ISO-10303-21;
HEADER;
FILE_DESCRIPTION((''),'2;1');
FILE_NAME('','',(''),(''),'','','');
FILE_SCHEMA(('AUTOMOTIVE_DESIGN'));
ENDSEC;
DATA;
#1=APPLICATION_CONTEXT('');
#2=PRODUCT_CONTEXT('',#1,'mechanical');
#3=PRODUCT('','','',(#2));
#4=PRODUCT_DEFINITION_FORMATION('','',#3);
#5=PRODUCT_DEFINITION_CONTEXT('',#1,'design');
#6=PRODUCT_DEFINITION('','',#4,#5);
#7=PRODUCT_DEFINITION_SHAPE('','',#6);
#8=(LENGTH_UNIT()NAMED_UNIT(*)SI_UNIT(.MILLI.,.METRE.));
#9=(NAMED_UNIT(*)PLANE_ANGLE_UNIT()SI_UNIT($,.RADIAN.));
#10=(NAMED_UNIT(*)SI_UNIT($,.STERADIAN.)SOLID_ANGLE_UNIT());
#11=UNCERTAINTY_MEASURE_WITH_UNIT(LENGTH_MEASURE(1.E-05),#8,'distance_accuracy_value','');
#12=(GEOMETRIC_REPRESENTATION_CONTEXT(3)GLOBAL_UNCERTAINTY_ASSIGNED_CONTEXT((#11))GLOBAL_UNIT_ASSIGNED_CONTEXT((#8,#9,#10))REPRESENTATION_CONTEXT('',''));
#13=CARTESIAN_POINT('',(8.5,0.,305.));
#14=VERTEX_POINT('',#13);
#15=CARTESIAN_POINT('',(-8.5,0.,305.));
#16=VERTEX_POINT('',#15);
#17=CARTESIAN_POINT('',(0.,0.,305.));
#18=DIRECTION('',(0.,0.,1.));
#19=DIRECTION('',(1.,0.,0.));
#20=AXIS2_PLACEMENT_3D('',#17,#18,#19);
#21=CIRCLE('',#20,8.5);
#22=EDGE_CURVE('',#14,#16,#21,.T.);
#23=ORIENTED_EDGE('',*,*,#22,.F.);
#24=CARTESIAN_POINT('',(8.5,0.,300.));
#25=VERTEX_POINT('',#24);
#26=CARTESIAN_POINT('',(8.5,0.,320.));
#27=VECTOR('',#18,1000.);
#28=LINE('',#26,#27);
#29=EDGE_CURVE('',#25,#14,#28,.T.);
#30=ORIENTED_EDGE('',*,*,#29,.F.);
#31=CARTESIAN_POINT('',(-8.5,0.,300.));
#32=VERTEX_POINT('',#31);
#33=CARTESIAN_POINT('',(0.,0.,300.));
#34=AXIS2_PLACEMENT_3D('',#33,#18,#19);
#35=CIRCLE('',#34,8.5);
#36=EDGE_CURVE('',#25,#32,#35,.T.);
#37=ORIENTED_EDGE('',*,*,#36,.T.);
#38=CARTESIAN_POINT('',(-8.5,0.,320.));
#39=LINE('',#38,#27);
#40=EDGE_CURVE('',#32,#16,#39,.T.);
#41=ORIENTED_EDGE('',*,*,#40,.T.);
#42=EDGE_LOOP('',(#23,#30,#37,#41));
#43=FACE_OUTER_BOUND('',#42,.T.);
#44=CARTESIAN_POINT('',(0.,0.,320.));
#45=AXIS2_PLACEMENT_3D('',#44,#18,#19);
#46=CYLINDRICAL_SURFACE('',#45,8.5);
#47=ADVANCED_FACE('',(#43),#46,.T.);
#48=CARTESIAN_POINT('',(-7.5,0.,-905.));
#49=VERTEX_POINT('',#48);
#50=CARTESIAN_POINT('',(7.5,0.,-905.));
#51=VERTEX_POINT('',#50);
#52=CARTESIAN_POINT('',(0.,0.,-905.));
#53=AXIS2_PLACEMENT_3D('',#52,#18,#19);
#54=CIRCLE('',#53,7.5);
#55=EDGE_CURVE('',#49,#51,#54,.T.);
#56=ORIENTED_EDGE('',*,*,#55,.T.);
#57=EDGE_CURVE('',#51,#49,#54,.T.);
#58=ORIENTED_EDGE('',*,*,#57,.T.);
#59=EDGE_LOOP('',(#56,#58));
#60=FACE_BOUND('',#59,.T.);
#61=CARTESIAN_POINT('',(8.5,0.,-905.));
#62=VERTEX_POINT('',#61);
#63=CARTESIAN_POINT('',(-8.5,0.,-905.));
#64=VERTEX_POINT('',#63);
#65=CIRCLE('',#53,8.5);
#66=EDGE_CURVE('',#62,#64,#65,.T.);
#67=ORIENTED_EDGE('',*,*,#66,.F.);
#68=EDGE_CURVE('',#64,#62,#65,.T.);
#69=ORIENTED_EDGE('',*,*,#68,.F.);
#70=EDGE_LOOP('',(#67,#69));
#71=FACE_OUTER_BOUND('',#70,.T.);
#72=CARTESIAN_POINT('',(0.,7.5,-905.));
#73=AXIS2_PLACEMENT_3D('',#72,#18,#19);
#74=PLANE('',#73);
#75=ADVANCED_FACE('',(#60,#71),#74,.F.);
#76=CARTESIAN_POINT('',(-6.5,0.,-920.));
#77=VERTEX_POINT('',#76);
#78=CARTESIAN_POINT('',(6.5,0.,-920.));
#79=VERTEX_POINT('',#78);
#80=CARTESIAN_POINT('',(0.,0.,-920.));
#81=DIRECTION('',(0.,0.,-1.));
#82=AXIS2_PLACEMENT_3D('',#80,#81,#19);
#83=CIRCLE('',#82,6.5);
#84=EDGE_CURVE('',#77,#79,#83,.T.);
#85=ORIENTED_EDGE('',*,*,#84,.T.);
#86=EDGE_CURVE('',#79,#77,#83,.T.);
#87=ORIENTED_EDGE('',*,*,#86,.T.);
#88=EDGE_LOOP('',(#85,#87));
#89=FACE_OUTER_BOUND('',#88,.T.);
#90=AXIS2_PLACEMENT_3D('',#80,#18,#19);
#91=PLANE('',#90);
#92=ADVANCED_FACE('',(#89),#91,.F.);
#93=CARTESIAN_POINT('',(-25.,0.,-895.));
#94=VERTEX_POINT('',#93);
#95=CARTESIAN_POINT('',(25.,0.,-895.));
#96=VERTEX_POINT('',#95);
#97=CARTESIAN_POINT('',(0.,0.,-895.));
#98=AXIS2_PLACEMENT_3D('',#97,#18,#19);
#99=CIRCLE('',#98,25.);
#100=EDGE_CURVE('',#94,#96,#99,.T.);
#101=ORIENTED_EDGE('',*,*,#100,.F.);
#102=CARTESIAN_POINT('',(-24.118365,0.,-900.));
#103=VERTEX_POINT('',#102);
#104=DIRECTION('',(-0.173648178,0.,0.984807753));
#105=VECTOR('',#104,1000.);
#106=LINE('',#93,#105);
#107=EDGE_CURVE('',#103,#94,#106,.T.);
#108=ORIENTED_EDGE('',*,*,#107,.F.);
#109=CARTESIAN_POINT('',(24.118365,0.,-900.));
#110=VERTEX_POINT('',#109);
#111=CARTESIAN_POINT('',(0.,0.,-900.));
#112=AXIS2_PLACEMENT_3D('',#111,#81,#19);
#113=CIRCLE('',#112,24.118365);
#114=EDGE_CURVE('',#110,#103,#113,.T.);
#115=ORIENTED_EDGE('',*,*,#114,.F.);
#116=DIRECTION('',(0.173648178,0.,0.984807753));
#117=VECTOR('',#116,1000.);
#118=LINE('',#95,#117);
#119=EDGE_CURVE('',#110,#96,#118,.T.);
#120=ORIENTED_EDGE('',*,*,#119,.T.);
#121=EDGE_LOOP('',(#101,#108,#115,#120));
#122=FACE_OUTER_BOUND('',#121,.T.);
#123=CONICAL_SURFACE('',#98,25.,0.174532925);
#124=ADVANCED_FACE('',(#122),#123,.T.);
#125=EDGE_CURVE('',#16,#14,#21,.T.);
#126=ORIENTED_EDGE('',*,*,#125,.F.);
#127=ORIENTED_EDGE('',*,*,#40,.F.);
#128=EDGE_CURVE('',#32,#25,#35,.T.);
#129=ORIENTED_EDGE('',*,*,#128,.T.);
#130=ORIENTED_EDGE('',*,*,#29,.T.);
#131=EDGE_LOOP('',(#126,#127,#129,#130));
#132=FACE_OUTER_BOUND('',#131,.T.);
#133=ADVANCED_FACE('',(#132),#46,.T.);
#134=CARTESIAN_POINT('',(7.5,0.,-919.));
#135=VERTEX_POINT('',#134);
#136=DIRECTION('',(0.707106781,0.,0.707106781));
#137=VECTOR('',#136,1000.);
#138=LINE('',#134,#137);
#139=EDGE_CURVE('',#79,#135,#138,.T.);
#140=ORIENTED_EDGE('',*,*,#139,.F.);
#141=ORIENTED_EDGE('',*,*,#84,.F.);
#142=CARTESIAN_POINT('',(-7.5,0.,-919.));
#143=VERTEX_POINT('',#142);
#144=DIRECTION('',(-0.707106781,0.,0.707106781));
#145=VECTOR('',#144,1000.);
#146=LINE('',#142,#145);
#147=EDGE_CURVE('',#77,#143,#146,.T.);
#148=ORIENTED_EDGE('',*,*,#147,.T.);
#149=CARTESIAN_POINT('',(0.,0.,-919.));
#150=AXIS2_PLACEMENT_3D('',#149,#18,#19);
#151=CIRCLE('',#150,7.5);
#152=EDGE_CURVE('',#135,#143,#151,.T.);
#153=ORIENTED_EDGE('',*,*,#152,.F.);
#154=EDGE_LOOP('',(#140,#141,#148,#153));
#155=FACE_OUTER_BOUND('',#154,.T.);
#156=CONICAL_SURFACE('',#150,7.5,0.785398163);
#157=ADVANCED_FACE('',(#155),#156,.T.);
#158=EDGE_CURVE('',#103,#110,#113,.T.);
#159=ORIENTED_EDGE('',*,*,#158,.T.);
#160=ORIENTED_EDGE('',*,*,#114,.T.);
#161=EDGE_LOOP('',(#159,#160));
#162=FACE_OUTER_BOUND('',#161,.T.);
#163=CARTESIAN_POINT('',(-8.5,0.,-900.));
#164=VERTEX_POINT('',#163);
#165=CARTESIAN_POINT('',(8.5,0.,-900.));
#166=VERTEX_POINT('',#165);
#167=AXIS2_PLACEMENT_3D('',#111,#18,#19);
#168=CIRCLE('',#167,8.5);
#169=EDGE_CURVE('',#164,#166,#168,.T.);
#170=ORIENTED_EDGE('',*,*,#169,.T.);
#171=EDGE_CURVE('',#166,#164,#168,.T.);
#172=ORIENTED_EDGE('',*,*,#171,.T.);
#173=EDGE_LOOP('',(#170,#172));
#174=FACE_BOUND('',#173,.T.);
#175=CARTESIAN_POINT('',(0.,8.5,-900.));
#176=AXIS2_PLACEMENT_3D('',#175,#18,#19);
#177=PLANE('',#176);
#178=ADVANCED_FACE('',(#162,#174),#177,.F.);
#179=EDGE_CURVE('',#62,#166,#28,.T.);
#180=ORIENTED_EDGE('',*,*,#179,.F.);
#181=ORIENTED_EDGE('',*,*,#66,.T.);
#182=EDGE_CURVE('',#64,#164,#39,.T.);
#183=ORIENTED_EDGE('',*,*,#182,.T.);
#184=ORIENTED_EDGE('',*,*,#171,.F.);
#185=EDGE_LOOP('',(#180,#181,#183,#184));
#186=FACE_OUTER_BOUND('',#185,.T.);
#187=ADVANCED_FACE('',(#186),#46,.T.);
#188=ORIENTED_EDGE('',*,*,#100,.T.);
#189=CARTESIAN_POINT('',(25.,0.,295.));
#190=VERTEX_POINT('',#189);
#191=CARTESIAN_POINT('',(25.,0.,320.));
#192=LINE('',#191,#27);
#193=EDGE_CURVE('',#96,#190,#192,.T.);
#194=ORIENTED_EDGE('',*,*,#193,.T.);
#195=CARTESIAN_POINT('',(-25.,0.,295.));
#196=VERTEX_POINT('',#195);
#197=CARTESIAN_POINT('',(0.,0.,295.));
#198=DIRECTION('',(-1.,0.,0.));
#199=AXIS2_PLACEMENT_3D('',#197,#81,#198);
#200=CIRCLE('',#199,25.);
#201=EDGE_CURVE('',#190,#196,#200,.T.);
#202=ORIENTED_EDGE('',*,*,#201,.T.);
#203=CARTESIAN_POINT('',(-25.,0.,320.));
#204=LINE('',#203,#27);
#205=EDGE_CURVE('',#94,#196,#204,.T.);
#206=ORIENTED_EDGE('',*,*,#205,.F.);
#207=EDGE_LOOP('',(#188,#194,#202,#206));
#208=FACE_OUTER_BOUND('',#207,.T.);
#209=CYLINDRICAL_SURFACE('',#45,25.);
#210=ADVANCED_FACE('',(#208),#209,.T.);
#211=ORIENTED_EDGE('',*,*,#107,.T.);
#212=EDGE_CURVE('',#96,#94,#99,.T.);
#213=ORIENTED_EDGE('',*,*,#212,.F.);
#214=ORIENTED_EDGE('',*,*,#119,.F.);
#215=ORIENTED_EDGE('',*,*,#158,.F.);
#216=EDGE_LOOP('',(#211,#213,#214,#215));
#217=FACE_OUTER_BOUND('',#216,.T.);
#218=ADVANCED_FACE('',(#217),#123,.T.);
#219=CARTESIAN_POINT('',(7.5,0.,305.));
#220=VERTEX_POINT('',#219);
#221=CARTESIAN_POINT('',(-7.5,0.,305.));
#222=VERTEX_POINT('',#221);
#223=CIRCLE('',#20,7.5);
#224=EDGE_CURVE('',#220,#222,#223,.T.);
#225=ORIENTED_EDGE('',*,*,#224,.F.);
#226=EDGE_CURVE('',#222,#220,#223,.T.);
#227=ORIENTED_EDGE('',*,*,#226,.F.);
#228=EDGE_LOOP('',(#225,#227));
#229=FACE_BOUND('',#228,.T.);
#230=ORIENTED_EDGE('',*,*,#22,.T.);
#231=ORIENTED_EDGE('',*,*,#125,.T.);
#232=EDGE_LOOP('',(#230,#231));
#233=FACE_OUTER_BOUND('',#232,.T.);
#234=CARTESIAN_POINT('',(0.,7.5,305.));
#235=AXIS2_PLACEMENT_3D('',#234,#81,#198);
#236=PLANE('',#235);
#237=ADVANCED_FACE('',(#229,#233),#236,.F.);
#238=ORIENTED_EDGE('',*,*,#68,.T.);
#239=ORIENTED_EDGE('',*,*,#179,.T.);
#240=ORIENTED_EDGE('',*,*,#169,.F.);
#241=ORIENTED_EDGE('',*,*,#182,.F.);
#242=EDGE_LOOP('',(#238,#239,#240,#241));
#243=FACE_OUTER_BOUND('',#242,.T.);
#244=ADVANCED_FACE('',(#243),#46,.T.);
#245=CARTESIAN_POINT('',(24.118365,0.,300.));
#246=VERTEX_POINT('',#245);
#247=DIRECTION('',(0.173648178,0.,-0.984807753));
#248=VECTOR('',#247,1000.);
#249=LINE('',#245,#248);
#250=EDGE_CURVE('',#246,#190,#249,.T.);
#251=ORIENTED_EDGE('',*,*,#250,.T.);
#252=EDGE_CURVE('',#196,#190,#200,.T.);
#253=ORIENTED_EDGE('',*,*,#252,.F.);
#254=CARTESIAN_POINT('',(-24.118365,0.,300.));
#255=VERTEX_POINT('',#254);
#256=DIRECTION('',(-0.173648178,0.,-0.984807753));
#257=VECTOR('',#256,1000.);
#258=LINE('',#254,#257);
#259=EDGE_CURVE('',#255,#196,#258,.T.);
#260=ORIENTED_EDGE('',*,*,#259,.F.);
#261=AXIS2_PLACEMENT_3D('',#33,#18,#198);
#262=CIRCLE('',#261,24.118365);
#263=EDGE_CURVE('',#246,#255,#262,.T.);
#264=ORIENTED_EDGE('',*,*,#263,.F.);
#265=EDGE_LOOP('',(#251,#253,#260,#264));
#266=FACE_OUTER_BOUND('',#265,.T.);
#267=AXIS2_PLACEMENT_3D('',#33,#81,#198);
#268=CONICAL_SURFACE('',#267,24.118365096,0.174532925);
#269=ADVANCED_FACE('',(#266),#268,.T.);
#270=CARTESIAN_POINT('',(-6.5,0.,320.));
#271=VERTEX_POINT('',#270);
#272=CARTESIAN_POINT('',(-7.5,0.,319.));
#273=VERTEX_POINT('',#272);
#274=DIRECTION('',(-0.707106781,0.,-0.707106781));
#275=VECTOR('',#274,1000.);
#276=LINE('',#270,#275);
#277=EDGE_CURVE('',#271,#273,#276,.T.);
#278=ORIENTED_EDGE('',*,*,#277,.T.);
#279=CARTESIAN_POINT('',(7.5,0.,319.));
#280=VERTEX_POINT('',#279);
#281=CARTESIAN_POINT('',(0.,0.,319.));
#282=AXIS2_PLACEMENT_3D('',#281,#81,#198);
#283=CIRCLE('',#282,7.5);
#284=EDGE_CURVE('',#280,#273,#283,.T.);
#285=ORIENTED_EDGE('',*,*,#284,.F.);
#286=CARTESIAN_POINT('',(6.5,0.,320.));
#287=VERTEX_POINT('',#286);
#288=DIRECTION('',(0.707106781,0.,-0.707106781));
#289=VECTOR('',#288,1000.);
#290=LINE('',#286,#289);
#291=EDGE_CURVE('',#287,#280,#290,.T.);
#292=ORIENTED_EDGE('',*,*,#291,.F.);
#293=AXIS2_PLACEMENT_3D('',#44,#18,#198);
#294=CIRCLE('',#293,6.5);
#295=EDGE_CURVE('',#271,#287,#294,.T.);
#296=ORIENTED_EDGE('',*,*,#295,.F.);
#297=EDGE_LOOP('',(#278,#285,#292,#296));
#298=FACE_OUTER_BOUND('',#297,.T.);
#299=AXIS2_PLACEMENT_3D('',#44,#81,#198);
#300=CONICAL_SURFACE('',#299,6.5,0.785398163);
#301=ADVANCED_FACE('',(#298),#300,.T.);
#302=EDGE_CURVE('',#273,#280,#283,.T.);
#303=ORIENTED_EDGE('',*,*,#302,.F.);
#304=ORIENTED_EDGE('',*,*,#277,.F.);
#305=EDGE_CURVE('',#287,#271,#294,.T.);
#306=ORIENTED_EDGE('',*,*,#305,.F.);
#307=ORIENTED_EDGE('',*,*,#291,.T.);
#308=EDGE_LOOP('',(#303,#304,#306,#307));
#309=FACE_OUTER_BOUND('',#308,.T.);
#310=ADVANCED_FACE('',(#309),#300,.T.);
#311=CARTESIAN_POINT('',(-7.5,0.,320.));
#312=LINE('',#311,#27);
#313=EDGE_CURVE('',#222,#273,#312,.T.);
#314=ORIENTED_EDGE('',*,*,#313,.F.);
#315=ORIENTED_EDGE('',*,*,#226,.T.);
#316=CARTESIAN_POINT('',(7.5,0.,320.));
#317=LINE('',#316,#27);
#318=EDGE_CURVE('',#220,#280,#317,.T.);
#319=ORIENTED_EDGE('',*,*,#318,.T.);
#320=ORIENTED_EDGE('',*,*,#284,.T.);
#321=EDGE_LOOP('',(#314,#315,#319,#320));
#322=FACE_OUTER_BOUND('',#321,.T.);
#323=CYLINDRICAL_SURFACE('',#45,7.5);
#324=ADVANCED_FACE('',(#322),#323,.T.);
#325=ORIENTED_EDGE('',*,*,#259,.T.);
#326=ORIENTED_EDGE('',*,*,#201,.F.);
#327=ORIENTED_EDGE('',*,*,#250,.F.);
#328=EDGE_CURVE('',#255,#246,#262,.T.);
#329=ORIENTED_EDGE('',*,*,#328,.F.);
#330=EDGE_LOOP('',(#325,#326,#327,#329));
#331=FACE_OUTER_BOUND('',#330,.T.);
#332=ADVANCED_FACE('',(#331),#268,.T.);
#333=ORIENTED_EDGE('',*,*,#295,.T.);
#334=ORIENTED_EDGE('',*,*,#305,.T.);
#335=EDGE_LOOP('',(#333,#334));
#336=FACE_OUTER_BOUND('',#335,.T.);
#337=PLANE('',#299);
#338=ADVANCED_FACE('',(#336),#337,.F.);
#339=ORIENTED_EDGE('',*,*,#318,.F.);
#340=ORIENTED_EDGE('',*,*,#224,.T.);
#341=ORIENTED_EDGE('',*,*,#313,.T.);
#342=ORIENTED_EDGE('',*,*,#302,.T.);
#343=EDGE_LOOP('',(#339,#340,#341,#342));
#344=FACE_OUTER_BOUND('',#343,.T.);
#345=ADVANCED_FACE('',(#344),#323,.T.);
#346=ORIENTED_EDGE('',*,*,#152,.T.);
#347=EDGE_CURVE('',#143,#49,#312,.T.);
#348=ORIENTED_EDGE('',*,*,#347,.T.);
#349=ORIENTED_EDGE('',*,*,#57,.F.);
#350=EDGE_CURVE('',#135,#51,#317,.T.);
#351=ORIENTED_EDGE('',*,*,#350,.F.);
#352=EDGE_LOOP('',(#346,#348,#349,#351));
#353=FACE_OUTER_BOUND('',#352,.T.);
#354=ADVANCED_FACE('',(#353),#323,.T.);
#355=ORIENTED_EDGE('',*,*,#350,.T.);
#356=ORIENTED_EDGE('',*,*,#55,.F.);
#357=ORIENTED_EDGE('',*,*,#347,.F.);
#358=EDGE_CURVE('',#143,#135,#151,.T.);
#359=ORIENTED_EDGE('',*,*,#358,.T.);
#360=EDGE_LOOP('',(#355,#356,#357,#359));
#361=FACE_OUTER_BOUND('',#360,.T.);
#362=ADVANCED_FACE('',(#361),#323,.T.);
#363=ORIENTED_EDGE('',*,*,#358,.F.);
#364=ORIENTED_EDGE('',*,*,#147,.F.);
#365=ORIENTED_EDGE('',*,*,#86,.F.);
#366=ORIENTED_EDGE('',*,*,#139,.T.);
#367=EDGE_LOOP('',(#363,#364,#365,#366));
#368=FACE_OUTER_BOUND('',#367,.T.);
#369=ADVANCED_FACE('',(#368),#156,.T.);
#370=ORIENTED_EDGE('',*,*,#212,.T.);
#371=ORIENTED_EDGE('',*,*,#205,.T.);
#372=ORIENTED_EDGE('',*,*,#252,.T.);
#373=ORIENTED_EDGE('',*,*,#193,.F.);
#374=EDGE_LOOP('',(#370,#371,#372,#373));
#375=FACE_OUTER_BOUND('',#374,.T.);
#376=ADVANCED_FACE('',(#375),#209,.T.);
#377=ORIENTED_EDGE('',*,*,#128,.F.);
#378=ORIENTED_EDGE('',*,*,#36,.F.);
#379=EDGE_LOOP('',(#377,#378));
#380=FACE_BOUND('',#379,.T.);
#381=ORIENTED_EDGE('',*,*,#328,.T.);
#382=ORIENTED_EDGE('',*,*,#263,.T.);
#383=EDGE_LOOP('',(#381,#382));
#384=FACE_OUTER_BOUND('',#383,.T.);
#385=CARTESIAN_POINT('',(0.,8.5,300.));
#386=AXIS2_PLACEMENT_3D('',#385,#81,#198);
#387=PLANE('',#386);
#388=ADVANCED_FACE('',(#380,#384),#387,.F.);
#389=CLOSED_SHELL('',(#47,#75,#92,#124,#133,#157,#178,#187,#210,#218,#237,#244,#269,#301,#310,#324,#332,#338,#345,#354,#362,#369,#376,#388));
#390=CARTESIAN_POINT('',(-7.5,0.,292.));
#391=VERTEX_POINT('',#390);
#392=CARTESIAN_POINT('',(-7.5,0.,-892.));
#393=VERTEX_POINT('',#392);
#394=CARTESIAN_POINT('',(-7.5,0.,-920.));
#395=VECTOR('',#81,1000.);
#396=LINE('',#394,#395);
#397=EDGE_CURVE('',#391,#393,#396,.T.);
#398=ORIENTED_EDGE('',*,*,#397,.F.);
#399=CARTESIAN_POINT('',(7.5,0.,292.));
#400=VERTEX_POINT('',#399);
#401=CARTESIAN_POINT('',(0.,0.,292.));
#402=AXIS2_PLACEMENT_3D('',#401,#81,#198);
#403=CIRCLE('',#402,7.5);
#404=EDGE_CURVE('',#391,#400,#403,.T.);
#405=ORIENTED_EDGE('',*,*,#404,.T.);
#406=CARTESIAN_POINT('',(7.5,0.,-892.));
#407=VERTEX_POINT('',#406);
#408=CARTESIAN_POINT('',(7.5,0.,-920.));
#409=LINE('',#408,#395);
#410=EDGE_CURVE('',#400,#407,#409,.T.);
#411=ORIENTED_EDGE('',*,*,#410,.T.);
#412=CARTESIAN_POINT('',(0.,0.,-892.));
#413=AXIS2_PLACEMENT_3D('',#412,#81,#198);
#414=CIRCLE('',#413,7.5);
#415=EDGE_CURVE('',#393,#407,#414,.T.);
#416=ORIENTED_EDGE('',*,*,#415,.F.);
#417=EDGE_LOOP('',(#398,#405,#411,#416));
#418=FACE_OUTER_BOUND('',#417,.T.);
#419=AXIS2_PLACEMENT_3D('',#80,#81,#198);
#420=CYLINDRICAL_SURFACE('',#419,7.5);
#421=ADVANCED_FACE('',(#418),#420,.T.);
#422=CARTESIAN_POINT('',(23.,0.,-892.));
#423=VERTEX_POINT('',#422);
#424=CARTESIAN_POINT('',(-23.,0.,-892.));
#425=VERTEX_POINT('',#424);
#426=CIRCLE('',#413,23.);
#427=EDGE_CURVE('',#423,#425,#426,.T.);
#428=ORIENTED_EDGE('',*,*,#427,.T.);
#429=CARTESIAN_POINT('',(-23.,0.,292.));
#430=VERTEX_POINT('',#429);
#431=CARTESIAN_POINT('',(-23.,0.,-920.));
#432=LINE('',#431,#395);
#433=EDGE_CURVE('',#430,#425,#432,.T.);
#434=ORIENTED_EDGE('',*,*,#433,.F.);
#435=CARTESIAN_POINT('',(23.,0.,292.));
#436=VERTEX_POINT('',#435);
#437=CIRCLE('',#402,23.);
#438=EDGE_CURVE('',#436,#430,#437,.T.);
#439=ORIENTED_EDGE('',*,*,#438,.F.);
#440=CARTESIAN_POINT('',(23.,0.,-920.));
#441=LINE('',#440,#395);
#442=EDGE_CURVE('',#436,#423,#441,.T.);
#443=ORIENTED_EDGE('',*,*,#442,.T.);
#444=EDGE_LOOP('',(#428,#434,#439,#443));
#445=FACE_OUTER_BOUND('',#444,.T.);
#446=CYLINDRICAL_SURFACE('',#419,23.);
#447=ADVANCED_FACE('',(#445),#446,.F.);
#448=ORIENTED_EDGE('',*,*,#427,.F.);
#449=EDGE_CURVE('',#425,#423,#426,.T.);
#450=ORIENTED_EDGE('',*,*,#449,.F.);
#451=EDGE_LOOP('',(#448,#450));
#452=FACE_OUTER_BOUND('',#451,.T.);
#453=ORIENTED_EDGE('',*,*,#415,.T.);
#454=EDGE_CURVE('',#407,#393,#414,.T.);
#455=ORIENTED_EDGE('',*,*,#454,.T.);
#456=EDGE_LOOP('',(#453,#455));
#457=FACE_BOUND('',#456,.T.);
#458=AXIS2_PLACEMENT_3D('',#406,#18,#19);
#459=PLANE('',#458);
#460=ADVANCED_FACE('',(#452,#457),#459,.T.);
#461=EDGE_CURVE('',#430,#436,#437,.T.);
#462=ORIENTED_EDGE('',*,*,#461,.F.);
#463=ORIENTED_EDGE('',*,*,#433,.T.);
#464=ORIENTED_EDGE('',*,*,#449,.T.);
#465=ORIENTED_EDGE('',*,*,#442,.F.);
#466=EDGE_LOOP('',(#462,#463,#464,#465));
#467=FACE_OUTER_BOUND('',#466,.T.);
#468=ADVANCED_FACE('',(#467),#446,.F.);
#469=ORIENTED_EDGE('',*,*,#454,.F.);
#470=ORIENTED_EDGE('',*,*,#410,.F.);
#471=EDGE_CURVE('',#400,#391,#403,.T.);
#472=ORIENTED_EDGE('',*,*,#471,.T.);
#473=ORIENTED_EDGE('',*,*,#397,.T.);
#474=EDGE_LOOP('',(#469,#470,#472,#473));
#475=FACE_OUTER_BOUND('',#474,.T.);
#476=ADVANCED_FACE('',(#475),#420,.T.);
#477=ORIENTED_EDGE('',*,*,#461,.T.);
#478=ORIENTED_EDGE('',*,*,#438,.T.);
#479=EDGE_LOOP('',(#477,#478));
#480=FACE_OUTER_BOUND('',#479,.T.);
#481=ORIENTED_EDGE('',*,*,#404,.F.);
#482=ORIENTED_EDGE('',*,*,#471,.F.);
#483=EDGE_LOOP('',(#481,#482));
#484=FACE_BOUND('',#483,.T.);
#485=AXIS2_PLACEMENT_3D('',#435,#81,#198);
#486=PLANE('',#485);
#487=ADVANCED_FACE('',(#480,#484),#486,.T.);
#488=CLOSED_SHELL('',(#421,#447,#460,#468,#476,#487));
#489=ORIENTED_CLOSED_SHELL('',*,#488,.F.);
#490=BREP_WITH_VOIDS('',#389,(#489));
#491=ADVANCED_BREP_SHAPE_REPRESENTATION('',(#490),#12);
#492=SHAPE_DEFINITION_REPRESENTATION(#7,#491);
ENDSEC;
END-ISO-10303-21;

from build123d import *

# Parameters (mm, degrees)
CHAMFER1_SIZE  = 5
CHAMFER1_SIZE2 = 0.881634904
CHAMFER2_SIZE  = 1
SKETCH5_W      = 15.5
SKETCH5_H      = 1184


with BuildPart() as part:
    # Sketch3 → Revolve1 (revolve)
    with BuildSketch(Plane(origin=(0, 0, 0), x_dir=(0, 0, -1), z_dir=(1, 0, 0)), mode=Mode.PRIVATE) as revolve1_sk:
        Polygon((-300, 25), (900, 25), (900, 8.5), (905, 8.5), (905, 7.5), (920, 7.5), (920, 0), (-320, 0), (-320, 7.5), (-305, 7.5), (-305, 8.5), (-300, 8.5), align=None)
    revolve(revolve1_sk.sketch.rotate(Axis((0, 0, 320), (0, 0, -1)), 90), axis=Axis((0, 0, 320), (0, 0, -1)))

    # Chamfer1
    chamfer1_edges = [part.edges().sort_by_distance(p)[0] for p in [
        (-25, 0, -900),
        (-25, 0, 300),
    ]]
    chamfer1_side = [part.faces().sort_by_distance(p)[0] for p in [
        (-25, 0, -300),
    ]]
    chamfer(chamfer1_edges, length=CHAMFER1_SIZE, length2=CHAMFER1_SIZE2, reference=chamfer1_side[0])

    # Chamfer2
    chamfer2_edges = [part.edges().sort_by_distance(p)[0] for p in [
        (-7.5, 0, -920),
        (-7.5, 0, 320),
    ]]
    chamfer(chamfer2_edges, length=CHAMFER2_SIZE)

    # Sketch5 → Cut-Revolve1 (revolve, cut)
    with BuildSketch(Plane(origin=(0, 0, 0), x_dir=(1, 0, 0), z_dir=(0, 1, 0)), mode=Mode.PRIVATE) as cut_revolve1_sk:
        with Locations((15.25, 300)):
            Rectangle(SKETCH5_W, SKETCH5_H)
    revolve(cut_revolve1_sk.sketch.rotate(Axis((0, 0, -920), (0, 0, 1)), 180), axis=Axis((0, 0, -920), (0, 0, 1)), mode=Mode.SUBTRACT)


solid = part.part
